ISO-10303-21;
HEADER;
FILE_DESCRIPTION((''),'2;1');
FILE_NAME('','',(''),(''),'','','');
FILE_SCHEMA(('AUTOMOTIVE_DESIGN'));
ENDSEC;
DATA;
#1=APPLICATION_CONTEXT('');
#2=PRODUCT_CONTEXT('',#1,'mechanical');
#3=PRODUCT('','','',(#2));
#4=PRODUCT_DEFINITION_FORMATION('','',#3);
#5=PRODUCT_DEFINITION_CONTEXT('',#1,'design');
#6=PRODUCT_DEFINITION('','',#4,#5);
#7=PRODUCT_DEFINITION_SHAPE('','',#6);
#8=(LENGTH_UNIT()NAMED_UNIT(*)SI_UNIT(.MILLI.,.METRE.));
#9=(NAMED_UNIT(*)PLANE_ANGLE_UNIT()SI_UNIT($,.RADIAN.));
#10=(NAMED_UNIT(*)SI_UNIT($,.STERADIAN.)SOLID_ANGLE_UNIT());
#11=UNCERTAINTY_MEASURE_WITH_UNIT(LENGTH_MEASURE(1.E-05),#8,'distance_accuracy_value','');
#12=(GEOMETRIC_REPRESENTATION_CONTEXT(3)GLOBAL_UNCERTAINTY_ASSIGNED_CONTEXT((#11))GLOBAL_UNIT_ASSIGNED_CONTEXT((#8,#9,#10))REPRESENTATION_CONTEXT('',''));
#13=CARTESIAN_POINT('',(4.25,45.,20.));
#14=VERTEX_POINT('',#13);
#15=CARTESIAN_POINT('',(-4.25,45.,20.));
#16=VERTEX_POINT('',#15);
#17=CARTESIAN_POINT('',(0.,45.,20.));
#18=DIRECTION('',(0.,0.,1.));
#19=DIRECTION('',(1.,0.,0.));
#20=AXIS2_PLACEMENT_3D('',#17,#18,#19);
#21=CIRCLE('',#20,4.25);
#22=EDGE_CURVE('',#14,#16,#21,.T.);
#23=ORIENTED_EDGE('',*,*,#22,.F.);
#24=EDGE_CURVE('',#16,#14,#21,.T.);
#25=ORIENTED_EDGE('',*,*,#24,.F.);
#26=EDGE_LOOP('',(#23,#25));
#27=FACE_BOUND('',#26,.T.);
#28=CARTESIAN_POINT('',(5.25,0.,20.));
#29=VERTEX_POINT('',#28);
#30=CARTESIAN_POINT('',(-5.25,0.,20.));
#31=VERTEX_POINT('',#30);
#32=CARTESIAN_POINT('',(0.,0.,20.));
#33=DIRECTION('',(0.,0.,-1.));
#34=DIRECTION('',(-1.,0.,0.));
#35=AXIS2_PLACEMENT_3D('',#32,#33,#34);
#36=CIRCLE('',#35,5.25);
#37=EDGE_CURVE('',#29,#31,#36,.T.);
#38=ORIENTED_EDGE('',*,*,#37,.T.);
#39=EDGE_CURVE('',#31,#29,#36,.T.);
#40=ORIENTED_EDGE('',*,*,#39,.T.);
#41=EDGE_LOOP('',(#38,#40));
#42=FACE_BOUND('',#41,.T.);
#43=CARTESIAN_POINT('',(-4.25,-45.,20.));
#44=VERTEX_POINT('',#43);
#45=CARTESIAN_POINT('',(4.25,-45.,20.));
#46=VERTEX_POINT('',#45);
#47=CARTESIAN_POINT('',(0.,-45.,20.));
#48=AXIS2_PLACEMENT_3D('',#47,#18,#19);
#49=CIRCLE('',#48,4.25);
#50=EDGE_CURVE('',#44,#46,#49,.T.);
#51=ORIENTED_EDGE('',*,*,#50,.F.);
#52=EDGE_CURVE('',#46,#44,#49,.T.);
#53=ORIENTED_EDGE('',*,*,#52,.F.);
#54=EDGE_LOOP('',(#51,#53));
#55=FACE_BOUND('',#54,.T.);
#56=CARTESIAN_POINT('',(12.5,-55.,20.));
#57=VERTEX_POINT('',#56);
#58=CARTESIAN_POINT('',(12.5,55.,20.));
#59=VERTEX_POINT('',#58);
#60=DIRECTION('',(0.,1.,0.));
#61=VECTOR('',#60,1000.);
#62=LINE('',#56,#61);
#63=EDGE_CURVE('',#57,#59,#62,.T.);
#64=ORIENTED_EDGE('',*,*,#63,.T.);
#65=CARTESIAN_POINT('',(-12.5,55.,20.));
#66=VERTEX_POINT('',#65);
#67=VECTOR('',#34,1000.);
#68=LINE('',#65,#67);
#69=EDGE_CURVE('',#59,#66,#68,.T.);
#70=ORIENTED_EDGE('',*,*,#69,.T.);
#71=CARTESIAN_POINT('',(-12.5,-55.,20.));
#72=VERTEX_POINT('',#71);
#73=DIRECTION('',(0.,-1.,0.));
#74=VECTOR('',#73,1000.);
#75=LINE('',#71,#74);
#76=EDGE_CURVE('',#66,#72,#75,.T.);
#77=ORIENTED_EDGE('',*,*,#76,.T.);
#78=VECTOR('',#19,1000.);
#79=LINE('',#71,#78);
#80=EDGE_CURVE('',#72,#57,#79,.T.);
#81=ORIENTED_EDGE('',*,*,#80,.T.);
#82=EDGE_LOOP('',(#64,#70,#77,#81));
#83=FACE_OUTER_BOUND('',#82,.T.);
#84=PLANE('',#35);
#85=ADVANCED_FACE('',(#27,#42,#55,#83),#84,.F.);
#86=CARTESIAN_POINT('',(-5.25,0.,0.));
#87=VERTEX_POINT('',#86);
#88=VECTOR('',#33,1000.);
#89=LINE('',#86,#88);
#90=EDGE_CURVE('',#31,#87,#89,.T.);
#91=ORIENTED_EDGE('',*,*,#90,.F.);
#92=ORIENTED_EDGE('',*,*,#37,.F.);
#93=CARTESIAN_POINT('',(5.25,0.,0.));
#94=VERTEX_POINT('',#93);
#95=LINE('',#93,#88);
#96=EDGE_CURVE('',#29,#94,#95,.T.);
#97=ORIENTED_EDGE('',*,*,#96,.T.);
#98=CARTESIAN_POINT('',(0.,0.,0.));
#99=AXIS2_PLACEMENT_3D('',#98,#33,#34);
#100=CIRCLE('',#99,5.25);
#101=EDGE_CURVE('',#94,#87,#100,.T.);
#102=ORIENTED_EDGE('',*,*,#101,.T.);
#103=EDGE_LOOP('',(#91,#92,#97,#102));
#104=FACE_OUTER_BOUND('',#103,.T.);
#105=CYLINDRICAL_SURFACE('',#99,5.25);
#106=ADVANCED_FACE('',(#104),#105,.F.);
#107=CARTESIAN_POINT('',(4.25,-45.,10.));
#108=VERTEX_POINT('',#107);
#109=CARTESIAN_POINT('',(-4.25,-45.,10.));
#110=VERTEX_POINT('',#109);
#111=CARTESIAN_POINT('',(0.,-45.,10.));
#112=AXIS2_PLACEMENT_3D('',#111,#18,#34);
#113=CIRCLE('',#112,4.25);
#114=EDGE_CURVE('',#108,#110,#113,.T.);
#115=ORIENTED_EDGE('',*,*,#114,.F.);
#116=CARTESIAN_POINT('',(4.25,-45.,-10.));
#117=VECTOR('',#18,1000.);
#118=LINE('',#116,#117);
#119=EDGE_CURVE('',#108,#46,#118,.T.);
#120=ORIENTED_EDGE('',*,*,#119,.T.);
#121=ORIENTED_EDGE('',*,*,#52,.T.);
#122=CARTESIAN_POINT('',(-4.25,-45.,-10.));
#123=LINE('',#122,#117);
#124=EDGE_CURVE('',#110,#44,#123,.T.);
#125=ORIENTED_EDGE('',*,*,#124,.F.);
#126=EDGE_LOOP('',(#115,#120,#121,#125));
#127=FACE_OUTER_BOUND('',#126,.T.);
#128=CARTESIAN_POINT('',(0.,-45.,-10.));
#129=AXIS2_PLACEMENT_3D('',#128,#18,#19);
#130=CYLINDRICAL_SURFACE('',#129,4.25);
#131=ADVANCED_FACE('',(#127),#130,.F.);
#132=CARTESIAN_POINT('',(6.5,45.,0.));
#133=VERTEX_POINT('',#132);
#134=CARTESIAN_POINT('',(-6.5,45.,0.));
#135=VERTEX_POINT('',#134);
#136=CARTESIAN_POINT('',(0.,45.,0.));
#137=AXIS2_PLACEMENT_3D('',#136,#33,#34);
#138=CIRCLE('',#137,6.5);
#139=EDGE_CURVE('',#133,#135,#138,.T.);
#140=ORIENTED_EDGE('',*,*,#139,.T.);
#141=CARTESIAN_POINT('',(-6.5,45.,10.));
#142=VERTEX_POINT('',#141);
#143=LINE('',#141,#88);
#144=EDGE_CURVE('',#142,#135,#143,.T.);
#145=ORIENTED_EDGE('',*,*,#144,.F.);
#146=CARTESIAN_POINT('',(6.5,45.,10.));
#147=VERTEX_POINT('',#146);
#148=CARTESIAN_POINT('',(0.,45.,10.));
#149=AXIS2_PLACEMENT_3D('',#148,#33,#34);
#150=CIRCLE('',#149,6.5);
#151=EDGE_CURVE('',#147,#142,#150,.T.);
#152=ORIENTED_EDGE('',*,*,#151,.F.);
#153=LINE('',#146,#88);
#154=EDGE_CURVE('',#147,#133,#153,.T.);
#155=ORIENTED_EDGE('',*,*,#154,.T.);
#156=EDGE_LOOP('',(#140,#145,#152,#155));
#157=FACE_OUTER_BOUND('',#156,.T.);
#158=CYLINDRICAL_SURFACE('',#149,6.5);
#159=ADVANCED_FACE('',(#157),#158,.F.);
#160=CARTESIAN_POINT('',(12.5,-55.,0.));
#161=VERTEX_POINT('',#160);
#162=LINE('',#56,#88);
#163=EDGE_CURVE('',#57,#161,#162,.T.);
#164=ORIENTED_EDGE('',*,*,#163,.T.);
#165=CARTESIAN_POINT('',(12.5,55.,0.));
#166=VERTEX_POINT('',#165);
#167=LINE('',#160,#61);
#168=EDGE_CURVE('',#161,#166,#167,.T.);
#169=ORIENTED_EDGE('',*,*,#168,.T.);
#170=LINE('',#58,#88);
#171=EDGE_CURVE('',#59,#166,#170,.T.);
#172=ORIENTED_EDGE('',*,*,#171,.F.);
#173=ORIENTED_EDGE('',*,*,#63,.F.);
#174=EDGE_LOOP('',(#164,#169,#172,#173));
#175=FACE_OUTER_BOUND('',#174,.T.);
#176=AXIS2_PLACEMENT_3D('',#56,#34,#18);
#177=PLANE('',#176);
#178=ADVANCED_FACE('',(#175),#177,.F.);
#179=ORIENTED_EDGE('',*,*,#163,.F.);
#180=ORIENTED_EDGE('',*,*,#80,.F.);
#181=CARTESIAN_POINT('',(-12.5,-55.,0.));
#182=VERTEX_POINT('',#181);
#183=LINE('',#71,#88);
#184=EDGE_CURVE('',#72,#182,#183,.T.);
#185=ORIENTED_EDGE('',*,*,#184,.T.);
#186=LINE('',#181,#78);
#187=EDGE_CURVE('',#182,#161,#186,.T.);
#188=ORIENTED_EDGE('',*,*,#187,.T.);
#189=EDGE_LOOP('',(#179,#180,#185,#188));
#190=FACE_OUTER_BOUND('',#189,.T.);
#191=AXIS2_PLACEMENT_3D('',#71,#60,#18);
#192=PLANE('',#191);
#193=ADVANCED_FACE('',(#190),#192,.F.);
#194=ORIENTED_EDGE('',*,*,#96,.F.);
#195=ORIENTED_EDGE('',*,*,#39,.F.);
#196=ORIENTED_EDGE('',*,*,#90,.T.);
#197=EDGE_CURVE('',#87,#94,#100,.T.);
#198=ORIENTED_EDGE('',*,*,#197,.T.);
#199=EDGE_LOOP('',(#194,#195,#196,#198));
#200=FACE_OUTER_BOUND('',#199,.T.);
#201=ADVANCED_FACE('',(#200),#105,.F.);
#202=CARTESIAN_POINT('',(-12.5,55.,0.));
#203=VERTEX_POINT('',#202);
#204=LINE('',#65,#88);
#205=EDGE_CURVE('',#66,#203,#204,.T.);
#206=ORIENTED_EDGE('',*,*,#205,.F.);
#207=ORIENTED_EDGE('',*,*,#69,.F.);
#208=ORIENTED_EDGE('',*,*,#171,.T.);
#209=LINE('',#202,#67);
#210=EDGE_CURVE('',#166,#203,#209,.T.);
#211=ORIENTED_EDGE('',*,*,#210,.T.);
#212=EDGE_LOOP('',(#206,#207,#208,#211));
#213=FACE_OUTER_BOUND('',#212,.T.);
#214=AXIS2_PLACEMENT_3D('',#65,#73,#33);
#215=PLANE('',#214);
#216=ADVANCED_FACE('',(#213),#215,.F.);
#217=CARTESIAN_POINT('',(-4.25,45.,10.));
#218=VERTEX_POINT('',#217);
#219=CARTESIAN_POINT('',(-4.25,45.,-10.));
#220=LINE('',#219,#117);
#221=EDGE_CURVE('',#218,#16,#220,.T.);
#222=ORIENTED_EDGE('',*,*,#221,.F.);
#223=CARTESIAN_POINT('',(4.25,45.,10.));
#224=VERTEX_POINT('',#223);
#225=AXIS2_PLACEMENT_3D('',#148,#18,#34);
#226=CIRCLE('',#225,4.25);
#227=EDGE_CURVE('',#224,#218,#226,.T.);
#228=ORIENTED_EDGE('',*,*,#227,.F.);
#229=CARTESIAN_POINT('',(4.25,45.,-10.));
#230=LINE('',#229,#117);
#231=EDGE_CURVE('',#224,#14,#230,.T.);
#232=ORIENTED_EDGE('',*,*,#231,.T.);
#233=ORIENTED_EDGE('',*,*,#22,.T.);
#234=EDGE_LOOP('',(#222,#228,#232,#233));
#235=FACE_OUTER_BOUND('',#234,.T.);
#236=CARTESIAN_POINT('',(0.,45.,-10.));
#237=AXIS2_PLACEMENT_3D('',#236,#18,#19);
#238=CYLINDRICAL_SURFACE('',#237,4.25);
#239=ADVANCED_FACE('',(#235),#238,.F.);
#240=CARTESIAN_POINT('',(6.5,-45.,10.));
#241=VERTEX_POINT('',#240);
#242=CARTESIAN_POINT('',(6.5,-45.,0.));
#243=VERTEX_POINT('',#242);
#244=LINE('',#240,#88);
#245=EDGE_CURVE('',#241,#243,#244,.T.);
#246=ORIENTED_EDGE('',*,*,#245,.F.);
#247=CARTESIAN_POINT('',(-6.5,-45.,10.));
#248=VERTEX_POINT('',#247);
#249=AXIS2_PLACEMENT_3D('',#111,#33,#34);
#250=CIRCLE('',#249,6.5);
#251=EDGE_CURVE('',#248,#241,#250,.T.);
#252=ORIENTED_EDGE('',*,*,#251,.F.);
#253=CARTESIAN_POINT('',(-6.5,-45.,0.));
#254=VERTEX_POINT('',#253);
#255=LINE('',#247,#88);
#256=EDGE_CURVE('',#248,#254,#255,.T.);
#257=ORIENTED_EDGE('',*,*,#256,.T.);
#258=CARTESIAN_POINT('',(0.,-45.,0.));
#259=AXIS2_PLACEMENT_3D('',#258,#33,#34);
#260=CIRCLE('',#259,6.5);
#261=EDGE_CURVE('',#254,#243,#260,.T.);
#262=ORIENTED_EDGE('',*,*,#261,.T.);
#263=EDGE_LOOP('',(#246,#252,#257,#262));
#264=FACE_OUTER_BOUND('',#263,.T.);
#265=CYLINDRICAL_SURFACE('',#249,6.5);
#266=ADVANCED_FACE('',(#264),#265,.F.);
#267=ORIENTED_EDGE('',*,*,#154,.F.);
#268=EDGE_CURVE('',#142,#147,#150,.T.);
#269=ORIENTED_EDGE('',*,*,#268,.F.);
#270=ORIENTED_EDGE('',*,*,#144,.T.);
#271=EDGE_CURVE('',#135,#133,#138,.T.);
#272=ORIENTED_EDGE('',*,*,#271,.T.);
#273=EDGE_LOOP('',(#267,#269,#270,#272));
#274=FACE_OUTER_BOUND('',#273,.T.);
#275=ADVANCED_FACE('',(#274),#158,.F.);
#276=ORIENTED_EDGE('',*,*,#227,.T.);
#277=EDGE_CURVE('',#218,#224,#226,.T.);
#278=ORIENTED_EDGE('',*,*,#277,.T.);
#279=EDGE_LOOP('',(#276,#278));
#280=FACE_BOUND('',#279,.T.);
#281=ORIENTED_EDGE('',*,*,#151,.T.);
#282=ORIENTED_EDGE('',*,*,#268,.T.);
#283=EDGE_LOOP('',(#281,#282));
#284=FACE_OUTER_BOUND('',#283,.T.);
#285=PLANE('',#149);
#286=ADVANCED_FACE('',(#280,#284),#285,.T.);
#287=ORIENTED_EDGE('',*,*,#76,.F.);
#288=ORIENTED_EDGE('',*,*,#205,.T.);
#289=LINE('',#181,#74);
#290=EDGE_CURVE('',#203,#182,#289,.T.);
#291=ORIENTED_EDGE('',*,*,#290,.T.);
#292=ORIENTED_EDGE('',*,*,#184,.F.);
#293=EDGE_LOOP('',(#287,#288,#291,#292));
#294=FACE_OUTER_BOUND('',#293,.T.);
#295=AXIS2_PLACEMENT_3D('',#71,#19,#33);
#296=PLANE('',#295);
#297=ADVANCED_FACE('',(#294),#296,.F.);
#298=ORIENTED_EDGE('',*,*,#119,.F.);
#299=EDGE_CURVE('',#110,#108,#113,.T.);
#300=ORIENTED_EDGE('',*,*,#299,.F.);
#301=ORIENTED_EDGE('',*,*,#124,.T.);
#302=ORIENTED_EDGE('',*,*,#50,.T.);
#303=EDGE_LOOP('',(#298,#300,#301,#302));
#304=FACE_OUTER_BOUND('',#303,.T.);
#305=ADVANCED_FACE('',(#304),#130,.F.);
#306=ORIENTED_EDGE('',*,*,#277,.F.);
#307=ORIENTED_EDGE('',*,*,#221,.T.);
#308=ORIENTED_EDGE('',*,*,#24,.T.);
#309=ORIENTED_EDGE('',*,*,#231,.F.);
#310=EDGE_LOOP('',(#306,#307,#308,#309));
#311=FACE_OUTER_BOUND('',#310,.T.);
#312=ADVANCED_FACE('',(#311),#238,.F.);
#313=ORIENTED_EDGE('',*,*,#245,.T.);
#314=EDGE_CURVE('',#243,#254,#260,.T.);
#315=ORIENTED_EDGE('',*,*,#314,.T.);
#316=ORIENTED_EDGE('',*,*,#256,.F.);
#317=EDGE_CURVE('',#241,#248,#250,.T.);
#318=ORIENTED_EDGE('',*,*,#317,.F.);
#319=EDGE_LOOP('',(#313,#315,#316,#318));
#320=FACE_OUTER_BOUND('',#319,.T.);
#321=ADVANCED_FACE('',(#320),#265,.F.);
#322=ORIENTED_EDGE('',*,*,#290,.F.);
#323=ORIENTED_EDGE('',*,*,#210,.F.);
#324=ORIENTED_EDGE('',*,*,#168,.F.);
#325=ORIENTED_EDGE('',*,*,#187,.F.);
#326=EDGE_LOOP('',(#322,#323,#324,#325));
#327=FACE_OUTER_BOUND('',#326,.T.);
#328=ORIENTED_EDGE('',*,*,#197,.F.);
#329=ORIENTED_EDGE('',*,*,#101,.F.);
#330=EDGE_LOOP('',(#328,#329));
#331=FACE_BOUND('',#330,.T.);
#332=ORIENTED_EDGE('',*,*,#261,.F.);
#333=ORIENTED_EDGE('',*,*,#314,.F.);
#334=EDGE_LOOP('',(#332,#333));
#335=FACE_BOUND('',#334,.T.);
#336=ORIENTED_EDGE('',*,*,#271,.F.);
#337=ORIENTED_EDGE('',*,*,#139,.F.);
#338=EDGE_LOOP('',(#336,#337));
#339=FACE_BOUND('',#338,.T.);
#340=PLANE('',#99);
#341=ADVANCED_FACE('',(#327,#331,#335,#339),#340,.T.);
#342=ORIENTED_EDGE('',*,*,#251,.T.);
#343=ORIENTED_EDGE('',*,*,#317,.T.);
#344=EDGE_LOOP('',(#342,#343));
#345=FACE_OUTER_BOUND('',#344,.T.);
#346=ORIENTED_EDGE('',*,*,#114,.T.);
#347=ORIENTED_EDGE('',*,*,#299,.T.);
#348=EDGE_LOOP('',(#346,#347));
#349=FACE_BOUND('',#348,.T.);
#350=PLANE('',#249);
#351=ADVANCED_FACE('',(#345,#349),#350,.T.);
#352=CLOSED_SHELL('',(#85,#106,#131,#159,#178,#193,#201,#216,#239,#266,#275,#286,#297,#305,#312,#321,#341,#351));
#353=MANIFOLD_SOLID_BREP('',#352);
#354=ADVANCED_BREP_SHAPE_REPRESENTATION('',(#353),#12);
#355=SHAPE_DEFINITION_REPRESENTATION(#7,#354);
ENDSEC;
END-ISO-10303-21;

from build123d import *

# Parameters (mm, degrees)
SKETCH1_W                   = 25
SKETCH1_H                   = 110
BOSS_EXTRUDE1_DEPTH         = 20
SKETCH3_R                   = 4.25
CUT_EXTRUDE1_DEPTH          = 30
SKETCH5_R                   = 6.5
CUT_EXTRUDE3_DEPTH          = 10
M12X1_25_TAPPED_HOLE1_D     = 10.5
M12X1_25_TAPPED_HOLE1_DEPTH = 30.25
M12X1_25_TAPPED_HOLE1_TIP   = 3.15451825


with BuildPart() as part:
    # Sketch1 → Boss-Extrude1 (new body)
    with BuildSketch(Plane.XY):
        Rectangle(SKETCH1_W, SKETCH1_H)
    extrude(amount=BOSS_EXTRUDE1_DEPTH)

    # Sketch3 → Cut-Extrude1 (cut)
    with BuildSketch(Plane.XY.offset(20)):
        with Locations((0, 45)):
            Circle(SKETCH3_R)
        with Locations((0, -45)):
            Circle(SKETCH3_R)
    extrude(amount=-CUT_EXTRUDE1_DEPTH, mode=Mode.SUBTRACT)

    # Sketch5 → Cut-Extrude3 (cut)
    with BuildSketch(Plane(origin=(0, 0, 0), x_dir=(-1, 0, 0), z_dir=(0, 0, -1))):
        with Locations((0, 45)):
            Circle(SKETCH5_R)
        with Locations((0, -45)):
            Circle(SKETCH5_R)
    extrude(amount=-CUT_EXTRUDE3_DEPTH, mode=Mode.SUBTRACT)

    # M12x1.25 Tapped Hole1
    with Locations(Plane(origin=(0, 0, 0), x_dir=(-1, 0, 0), z_dir=(0, 0, -1))):
        with Locations((0, 0)):
            Hole(M12X1_25_TAPPED_HOLE1_D / 2, depth=M12X1_25_TAPPED_HOLE1_DEPTH)
            with Locations((0, 0, -(M12X1_25_TAPPED_HOLE1_DEPTH + M12X1_25_TAPPED_HOLE1_TIP / 2))):  # 118° drill point
                Cone(0, M12X1_25_TAPPED_HOLE1_D / 2, M12X1_25_TAPPED_HOLE1_TIP, mode=Mode.SUBTRACT)


solid = part.part
